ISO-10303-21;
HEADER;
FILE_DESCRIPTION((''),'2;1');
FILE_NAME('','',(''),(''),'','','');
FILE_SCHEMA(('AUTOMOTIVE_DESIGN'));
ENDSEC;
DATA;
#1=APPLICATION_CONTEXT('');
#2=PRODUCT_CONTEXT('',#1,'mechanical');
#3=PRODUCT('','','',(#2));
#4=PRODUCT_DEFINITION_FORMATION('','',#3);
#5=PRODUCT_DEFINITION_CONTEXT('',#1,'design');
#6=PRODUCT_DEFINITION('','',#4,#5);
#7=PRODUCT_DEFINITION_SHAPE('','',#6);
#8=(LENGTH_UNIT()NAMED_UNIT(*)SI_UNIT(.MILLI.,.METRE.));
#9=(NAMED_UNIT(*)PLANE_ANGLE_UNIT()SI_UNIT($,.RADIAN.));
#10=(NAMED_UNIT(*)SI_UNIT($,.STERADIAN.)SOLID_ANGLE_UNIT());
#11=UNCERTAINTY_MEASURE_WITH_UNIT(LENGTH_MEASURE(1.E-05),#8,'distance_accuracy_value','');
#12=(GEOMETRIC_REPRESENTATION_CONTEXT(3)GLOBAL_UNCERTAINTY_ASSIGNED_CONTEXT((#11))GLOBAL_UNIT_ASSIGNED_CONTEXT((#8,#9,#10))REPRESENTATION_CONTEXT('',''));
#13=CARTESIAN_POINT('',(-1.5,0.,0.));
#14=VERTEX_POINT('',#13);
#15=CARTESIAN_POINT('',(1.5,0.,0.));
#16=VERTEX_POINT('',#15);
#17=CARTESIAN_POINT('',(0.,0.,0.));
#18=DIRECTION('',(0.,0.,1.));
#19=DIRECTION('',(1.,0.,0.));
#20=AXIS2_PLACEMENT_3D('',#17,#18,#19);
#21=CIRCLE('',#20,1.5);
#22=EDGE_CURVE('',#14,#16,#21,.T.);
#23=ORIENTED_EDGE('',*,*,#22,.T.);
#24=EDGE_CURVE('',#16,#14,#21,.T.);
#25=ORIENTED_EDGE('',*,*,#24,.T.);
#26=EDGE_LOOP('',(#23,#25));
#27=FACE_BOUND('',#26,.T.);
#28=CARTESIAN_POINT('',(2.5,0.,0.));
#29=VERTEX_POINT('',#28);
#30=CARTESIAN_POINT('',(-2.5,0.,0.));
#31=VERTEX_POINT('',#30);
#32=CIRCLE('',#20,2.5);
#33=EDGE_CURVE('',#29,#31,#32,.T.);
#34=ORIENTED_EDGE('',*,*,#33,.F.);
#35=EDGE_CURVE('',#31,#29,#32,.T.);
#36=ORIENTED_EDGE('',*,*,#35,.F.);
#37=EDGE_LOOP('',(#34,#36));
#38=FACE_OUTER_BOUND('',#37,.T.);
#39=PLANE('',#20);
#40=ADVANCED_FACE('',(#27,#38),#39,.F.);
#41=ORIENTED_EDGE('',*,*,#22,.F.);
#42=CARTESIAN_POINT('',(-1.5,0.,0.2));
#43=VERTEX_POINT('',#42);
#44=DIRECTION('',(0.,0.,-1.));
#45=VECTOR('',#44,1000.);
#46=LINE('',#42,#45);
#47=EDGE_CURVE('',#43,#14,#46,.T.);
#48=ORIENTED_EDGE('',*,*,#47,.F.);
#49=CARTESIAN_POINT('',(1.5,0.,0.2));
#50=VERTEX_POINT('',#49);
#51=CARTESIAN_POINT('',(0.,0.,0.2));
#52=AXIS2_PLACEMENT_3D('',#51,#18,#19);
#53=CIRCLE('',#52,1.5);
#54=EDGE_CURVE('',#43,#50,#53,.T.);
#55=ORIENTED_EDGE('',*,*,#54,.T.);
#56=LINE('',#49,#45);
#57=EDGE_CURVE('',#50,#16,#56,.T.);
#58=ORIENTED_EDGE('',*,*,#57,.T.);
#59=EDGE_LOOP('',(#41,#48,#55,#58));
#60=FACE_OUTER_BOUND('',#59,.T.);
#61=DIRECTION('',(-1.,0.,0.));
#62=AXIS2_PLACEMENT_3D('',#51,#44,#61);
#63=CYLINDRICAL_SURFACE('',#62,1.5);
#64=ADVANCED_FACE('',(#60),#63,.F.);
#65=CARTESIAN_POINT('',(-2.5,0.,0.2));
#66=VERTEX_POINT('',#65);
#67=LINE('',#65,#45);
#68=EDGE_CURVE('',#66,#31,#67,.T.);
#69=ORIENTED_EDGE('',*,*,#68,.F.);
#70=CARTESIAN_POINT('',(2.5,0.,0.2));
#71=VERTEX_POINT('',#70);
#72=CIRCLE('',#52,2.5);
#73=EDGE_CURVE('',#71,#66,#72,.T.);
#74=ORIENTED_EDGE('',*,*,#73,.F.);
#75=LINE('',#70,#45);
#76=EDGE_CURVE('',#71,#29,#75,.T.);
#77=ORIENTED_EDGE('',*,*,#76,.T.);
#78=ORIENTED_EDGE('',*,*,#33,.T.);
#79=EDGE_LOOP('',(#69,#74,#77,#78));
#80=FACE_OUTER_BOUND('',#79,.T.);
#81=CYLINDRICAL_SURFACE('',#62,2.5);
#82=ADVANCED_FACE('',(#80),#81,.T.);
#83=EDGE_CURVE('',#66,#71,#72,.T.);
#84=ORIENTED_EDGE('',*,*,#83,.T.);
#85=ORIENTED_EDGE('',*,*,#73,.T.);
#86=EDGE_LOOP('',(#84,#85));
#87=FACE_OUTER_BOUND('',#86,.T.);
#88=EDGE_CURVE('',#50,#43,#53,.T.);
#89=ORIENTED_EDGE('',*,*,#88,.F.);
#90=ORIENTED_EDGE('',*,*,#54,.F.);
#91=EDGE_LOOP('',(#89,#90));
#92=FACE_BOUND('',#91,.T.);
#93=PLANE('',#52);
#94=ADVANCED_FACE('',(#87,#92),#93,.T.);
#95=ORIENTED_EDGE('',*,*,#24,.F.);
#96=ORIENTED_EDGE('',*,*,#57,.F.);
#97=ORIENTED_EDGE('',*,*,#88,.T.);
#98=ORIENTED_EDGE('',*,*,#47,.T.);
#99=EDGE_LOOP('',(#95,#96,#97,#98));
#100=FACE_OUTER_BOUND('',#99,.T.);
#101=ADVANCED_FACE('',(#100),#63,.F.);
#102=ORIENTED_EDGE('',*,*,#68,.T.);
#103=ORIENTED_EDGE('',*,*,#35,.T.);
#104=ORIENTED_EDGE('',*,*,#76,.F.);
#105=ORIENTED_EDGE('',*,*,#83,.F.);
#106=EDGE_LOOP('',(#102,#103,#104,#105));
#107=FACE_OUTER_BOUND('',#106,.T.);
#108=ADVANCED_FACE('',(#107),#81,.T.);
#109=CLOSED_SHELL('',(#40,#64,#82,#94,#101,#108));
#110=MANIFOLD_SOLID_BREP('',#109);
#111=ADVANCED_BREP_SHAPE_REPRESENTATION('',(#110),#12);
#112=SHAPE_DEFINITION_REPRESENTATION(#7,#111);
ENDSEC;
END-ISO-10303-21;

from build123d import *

# Parameters (mm, degrees)
SKETCH1_R           = 2.5
SKETCH1_R_2         = 1.5
BOSS_EXTRUDE1_DEPTH = 0.2


with BuildPart() as part:
    # Sketch1 → Boss-Extrude1 (new body)
    with BuildSketch(Plane.XY):
        Circle(SKETCH1_R)
        Circle(SKETCH1_R_2, mode=Mode.SUBTRACT)
    extrude(amount=BOSS_EXTRUDE1_DEPTH)


solid = part.part
